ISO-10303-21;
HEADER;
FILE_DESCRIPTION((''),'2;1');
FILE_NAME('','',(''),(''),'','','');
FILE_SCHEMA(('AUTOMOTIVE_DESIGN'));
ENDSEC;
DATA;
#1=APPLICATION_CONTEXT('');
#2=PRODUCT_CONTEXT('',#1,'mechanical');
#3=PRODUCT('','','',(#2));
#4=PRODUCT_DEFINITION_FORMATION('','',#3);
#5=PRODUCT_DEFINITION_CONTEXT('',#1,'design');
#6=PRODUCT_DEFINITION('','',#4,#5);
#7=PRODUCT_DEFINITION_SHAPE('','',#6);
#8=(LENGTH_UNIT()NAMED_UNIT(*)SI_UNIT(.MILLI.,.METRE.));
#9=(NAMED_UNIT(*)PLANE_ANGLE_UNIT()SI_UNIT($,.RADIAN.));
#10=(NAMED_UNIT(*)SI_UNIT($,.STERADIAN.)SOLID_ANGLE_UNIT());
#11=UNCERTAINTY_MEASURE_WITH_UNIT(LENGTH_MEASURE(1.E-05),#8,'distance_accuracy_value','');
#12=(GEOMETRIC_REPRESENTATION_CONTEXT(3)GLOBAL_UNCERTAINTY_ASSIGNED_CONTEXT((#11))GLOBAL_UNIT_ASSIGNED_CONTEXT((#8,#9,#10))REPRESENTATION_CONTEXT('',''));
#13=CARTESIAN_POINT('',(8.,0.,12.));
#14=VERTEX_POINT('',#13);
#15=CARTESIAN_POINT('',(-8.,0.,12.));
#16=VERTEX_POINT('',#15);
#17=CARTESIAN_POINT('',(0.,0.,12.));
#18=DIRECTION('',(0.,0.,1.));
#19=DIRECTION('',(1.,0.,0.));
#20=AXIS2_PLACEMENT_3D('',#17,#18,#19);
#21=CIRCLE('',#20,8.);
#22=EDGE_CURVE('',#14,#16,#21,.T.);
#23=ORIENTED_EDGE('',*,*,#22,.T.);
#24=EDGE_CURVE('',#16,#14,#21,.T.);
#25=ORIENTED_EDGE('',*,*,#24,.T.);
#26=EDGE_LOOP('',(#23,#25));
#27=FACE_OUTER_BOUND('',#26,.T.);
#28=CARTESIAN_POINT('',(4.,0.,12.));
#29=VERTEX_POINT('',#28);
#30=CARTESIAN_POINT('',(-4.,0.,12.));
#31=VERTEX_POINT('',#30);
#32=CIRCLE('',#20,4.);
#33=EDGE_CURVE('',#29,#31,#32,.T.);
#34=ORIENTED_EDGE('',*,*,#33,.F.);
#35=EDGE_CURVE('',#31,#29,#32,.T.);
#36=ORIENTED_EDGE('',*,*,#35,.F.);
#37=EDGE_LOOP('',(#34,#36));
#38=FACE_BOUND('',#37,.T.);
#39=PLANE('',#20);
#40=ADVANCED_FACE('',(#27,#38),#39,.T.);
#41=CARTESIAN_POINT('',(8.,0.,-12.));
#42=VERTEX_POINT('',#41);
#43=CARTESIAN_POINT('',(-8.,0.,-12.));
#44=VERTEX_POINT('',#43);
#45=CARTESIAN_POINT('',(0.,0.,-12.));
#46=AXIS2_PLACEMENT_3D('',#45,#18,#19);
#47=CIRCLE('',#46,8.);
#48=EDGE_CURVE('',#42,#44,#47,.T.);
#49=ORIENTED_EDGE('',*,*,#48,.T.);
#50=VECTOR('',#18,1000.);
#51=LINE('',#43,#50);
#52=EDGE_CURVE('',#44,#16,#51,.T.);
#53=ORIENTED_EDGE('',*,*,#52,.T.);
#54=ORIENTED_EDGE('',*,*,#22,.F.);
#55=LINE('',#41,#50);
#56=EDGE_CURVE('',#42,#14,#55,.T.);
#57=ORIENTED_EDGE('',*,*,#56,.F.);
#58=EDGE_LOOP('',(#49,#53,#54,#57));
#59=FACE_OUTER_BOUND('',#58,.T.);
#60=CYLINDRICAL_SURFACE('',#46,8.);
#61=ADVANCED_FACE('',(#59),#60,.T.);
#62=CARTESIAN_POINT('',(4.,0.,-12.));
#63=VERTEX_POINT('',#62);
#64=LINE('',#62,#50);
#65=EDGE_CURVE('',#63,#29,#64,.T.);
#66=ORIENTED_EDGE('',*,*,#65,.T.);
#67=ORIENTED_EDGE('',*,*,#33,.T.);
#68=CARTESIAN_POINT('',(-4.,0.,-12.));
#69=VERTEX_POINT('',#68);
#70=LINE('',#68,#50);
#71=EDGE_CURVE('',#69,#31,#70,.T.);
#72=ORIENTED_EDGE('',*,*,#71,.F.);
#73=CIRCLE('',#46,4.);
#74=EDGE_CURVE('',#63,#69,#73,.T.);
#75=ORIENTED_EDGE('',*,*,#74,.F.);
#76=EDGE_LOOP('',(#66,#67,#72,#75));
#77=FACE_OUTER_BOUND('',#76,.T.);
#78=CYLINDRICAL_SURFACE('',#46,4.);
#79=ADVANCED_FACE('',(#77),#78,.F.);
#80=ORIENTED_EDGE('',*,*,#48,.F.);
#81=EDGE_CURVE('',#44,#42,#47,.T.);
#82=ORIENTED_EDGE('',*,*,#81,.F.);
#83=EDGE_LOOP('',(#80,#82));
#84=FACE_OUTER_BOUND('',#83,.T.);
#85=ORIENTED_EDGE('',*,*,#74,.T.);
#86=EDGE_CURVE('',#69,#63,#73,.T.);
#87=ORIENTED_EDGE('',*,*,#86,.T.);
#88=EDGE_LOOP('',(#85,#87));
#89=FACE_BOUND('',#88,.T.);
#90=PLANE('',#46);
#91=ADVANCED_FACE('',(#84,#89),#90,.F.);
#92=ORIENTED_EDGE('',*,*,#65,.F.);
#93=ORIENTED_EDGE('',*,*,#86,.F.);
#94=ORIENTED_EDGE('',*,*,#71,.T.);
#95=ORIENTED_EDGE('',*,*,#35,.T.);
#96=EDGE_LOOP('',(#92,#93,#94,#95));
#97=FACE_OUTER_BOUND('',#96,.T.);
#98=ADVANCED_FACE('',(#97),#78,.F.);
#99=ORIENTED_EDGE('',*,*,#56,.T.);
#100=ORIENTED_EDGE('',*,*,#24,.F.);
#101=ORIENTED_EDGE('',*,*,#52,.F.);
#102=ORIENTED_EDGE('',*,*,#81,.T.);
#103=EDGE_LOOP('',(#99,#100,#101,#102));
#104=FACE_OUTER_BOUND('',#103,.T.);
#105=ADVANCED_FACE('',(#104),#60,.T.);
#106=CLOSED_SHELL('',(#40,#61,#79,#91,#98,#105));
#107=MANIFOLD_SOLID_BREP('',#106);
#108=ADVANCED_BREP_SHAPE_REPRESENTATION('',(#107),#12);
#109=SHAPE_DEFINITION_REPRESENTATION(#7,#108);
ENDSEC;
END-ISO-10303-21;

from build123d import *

# Parameters (mm, degrees)
SKETCH_1_R      = 8
SKETCH_1_R_2    = 4
EXTRUDE_1_DEPTH = 12


with BuildPart() as part:
    # 草图1 → 凸台-拉伸1 (new, symmetric)
    with BuildSketch(Plane.XY):
        Circle(SKETCH_1_R)
        Circle(SKETCH_1_R_2, mode=Mode.SUBTRACT)
    extrude(amount=EXTRUDE_1_DEPTH, both=True)


solid = part.part
